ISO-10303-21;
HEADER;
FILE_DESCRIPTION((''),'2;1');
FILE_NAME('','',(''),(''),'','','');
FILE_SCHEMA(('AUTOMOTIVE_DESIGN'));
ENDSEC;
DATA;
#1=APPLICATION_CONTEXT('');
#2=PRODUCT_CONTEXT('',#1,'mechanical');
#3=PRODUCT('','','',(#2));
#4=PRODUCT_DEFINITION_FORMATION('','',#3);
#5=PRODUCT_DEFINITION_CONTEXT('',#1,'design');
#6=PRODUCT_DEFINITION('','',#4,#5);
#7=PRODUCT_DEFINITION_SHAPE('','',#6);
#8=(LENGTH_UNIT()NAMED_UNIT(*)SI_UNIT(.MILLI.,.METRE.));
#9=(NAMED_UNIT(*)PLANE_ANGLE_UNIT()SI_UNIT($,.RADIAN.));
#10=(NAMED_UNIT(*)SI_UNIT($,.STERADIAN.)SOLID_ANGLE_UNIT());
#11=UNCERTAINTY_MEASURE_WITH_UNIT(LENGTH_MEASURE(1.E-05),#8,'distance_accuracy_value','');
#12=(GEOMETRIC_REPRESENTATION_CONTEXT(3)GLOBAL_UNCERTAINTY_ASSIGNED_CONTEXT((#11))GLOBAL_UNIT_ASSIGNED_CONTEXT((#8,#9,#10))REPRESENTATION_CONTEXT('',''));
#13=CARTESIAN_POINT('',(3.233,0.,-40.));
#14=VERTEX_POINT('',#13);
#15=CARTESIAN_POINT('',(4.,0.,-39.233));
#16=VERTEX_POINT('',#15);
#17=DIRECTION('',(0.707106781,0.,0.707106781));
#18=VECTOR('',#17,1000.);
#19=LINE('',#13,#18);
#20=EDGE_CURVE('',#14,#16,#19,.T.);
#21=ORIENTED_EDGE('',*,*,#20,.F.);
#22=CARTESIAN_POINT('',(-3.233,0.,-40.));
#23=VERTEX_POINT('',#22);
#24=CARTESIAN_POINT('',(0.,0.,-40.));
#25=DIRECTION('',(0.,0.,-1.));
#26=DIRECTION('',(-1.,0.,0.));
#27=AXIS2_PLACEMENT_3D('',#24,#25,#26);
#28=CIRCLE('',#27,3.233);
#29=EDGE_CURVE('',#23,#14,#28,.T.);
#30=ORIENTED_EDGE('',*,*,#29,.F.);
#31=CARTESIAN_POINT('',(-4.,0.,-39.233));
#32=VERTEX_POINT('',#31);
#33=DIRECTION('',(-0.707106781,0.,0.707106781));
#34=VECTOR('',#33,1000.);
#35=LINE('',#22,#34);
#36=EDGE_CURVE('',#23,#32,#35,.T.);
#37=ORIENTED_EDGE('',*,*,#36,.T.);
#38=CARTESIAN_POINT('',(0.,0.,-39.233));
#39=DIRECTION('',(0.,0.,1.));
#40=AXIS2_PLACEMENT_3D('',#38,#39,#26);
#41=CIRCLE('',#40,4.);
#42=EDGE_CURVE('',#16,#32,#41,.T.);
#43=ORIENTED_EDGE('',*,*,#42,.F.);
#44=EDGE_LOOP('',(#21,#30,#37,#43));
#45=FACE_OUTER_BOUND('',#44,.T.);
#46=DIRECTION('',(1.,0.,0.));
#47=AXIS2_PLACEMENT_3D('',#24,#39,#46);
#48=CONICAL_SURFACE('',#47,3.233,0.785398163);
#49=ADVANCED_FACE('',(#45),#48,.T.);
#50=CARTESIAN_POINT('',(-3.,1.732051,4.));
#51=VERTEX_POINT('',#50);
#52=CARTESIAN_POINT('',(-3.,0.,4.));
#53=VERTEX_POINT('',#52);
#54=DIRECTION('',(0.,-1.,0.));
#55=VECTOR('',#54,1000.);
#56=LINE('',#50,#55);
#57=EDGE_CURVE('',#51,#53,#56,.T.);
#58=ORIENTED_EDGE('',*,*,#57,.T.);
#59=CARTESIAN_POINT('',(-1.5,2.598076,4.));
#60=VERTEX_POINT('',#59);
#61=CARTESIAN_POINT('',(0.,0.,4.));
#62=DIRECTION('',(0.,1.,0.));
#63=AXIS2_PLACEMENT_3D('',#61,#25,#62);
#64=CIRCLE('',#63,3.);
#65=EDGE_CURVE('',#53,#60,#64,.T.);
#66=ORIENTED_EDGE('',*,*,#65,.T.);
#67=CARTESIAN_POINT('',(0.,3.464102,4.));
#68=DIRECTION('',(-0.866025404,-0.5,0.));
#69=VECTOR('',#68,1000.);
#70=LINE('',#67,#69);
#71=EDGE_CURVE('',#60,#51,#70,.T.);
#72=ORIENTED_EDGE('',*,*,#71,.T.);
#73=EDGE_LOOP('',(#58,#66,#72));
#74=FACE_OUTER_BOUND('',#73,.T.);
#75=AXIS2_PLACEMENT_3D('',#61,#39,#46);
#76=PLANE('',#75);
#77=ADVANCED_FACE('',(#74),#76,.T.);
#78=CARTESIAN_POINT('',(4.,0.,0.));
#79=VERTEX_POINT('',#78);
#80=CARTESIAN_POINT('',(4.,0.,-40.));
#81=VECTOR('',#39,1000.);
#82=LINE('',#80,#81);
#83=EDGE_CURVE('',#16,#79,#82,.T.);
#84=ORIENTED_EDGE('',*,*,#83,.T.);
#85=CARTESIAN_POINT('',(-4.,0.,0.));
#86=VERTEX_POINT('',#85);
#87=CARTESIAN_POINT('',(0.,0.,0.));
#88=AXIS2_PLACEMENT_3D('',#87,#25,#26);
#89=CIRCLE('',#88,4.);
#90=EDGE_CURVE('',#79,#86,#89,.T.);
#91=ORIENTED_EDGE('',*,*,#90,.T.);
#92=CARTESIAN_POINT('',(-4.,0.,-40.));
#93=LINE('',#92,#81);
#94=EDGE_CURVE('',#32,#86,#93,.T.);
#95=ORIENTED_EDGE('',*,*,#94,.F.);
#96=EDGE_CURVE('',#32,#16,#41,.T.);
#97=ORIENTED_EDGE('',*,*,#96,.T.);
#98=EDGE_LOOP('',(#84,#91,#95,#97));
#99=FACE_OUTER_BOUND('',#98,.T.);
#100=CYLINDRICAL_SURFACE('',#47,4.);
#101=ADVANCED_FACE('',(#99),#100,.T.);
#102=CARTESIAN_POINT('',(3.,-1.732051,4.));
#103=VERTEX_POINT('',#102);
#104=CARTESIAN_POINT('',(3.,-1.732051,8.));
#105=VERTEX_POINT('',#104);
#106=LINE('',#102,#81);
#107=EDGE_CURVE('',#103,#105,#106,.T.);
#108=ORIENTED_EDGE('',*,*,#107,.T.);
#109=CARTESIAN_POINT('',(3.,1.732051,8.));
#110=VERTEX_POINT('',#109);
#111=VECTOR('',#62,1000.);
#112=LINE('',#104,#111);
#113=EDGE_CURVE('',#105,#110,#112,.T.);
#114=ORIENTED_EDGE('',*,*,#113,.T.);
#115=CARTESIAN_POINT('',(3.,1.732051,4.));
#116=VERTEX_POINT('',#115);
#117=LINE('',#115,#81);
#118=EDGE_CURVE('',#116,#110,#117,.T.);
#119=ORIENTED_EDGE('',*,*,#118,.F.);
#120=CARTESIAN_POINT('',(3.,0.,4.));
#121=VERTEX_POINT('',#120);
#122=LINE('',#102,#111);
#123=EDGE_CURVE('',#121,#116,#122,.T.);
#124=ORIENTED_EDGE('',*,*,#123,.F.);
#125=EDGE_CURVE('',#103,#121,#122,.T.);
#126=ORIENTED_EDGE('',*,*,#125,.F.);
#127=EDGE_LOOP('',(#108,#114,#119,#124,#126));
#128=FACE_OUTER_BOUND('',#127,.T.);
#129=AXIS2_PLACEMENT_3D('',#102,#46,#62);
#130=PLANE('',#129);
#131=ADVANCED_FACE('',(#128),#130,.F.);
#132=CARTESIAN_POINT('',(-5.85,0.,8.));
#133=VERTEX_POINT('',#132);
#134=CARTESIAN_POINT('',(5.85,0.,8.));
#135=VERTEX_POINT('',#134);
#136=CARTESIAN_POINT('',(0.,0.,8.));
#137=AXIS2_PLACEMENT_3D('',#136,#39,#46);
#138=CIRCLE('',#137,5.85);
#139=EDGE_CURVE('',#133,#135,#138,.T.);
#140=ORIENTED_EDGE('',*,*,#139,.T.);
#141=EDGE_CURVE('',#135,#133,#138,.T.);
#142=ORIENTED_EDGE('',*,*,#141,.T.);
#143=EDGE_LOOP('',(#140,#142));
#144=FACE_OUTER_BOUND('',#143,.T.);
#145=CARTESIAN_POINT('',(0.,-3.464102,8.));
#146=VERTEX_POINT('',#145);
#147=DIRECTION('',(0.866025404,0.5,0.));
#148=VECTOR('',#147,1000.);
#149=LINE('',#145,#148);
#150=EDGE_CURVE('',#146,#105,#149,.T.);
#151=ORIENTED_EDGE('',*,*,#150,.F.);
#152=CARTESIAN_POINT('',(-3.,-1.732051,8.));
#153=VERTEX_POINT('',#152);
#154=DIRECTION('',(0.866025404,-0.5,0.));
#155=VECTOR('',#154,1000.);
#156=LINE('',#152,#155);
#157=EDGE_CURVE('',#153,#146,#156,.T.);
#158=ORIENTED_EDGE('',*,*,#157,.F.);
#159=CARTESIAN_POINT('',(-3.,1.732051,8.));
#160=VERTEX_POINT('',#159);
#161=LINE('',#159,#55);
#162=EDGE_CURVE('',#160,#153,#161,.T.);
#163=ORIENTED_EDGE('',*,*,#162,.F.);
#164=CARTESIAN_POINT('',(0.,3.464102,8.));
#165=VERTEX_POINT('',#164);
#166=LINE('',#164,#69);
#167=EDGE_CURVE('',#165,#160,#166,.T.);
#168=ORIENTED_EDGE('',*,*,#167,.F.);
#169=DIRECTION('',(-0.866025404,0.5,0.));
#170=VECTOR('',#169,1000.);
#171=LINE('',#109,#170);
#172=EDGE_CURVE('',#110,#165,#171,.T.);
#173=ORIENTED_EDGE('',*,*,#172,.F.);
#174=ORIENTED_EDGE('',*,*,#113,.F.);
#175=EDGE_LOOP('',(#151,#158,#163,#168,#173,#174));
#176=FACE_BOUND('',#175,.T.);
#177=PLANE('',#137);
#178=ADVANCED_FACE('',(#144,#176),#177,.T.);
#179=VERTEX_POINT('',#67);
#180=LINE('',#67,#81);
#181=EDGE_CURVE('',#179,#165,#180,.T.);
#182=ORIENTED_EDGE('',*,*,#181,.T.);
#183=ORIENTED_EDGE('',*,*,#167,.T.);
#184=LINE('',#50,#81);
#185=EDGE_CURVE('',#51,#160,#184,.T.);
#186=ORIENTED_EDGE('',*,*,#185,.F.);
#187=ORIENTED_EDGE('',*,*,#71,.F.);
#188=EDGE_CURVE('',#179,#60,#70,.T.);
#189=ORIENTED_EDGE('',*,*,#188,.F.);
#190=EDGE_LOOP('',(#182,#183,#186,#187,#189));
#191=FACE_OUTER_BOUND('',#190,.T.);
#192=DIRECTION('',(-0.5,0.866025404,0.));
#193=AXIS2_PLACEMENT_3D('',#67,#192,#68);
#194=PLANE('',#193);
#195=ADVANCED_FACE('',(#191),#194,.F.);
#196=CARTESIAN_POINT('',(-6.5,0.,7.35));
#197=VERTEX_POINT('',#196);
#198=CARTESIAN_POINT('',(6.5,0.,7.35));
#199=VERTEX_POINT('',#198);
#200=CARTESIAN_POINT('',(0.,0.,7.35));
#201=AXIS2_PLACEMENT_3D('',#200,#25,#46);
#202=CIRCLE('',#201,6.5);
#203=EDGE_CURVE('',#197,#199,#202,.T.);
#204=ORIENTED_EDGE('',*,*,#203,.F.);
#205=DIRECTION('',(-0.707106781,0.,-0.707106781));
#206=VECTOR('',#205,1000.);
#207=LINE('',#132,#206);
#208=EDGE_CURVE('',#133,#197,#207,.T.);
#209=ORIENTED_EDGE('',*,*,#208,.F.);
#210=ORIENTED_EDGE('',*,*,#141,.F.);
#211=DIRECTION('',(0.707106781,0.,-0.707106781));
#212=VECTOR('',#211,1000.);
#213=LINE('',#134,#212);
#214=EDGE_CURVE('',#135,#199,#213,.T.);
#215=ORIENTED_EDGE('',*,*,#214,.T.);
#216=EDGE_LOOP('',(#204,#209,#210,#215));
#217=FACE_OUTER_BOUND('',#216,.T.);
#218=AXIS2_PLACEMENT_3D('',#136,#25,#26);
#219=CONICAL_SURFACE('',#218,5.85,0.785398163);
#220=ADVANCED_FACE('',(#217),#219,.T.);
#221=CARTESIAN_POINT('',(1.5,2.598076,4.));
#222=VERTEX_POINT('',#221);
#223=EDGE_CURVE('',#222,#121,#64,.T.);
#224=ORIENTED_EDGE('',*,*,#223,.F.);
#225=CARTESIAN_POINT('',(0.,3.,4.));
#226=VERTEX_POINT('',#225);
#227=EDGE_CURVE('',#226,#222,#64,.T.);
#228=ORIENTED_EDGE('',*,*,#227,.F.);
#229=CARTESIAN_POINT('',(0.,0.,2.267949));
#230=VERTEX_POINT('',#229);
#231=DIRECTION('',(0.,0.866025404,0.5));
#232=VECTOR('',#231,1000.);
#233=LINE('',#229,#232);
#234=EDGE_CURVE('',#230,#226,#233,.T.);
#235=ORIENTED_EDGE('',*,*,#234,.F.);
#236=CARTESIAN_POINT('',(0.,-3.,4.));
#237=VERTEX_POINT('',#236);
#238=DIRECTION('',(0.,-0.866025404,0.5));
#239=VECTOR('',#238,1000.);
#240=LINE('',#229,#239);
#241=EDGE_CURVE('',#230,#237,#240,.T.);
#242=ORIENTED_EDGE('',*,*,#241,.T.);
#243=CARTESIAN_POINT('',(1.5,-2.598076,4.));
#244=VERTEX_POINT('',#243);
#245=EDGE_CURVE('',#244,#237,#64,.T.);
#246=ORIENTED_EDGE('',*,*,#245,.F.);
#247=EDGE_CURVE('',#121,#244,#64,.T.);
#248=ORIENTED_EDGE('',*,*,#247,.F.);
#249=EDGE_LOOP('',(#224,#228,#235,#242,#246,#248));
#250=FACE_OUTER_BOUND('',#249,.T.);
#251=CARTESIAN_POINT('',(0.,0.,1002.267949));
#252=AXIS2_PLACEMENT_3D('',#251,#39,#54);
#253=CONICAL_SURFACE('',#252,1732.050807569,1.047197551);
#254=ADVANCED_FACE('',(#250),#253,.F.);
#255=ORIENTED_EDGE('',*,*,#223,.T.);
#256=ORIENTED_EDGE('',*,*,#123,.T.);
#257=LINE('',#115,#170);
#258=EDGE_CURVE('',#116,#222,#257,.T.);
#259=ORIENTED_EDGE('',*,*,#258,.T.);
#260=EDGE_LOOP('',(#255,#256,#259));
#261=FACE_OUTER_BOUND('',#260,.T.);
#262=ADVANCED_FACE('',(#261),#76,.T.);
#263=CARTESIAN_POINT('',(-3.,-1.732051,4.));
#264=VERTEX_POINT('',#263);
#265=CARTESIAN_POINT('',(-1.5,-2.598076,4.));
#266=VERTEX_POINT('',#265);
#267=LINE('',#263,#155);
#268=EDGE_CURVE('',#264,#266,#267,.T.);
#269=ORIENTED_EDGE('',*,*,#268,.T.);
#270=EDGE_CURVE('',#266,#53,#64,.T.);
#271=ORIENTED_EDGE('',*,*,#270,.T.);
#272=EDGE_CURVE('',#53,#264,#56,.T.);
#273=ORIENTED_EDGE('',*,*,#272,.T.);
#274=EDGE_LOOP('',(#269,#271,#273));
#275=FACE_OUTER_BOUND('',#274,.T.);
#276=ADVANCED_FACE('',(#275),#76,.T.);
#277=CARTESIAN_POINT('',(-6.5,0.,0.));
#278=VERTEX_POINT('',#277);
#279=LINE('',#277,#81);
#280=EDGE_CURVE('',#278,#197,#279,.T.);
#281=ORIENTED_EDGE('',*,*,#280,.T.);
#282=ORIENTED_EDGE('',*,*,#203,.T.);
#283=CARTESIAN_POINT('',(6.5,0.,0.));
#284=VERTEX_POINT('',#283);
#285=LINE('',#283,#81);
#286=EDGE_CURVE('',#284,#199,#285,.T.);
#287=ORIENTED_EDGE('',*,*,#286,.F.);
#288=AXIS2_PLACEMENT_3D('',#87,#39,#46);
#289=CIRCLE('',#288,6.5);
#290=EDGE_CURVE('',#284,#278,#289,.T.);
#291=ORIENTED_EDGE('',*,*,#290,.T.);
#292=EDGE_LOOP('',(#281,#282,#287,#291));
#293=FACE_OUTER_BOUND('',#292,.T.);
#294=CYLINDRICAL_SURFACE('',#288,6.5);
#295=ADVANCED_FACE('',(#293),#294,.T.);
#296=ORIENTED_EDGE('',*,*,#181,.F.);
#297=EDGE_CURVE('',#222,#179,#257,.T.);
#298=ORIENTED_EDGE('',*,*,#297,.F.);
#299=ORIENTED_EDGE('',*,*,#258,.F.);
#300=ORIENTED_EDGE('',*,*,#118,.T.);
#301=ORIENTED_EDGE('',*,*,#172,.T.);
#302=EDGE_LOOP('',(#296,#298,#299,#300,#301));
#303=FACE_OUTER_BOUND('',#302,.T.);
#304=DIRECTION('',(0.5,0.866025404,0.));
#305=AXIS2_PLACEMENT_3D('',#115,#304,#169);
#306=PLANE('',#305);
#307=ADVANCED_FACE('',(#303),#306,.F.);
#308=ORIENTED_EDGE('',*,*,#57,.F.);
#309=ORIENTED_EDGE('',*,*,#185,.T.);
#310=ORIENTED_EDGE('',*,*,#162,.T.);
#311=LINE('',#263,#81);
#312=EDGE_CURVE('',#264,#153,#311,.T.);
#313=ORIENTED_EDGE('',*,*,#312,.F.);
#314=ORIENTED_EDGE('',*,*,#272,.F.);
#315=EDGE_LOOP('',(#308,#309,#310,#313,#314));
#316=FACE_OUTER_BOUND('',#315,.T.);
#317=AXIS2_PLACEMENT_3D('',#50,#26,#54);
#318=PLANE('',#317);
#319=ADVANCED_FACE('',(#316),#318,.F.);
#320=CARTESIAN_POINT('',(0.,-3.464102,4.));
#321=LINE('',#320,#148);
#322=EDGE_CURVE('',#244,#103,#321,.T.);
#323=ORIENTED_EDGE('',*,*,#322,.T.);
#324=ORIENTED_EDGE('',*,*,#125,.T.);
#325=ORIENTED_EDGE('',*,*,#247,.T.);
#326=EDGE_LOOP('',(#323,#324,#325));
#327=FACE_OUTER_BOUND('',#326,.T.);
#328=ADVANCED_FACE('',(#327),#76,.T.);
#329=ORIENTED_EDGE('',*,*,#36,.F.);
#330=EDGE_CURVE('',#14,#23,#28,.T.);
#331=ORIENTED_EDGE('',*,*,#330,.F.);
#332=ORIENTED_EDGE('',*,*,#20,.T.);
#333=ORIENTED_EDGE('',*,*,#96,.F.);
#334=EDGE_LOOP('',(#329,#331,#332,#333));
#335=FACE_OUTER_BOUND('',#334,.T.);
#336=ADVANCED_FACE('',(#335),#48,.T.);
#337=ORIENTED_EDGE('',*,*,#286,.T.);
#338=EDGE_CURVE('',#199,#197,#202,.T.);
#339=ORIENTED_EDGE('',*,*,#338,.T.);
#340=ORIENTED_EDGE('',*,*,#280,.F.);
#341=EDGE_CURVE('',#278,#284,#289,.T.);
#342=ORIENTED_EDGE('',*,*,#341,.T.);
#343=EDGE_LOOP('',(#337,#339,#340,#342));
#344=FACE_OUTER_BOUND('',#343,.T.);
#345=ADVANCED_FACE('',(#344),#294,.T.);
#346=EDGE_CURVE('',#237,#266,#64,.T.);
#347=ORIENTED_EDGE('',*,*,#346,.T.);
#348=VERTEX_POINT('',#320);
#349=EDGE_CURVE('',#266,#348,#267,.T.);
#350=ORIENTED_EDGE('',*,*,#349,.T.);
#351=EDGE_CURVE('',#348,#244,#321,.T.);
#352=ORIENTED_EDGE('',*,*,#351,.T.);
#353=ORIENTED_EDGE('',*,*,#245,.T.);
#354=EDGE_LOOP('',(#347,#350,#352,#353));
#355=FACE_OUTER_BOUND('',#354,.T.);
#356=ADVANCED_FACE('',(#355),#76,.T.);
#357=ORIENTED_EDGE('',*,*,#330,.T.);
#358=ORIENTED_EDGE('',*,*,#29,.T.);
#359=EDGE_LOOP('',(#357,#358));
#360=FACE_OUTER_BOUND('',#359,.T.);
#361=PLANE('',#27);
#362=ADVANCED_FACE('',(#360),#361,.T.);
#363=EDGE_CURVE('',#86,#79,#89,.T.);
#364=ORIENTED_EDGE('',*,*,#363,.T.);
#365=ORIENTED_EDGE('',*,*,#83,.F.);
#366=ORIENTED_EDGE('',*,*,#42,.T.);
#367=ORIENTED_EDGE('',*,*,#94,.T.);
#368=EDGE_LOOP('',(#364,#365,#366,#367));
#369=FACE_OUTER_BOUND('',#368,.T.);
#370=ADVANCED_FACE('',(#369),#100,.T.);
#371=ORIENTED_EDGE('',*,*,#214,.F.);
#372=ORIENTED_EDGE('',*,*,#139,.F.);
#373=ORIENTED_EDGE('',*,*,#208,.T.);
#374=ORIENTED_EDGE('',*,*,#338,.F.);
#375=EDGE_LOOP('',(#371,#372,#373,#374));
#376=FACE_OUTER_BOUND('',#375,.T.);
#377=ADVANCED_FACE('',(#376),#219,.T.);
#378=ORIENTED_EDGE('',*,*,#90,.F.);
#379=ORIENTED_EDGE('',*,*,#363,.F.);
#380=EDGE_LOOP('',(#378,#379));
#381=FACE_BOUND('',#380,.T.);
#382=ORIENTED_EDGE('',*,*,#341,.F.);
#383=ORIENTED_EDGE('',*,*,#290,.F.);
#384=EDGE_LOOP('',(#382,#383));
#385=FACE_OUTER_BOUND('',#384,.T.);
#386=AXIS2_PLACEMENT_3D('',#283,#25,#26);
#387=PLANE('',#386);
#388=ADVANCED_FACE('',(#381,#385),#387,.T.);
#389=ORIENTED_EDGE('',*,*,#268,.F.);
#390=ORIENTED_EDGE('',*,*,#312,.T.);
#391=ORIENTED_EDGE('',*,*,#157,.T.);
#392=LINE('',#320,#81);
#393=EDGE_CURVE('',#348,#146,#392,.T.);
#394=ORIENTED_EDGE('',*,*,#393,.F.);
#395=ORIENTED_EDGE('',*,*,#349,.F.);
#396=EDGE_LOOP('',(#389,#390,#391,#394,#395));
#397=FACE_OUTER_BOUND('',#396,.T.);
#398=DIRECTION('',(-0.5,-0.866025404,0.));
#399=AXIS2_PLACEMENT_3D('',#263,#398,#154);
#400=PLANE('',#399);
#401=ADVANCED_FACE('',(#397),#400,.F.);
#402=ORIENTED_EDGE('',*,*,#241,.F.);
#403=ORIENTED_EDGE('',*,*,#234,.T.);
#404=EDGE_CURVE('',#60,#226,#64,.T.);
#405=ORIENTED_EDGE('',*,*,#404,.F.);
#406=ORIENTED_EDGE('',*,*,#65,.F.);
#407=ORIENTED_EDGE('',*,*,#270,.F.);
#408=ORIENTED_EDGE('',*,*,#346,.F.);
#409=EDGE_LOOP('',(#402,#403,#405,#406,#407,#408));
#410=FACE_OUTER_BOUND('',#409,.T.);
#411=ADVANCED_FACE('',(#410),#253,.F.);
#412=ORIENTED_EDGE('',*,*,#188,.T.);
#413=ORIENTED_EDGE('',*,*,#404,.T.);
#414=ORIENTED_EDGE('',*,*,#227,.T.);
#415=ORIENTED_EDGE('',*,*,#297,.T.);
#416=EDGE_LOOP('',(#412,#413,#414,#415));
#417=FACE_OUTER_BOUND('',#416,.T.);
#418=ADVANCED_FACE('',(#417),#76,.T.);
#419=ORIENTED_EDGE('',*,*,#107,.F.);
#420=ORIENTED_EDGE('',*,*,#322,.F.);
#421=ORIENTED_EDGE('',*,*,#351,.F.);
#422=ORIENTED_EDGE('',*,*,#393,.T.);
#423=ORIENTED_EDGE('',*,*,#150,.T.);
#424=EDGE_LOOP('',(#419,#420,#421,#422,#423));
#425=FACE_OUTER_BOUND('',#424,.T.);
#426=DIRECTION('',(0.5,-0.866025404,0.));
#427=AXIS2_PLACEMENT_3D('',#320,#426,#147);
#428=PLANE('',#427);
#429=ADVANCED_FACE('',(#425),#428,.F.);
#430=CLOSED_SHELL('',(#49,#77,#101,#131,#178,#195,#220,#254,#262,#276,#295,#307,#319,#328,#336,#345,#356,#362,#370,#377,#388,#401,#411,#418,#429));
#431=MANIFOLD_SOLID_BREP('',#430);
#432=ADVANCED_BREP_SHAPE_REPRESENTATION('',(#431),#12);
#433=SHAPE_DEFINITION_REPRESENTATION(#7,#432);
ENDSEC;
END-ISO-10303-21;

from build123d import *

# Parameters (mm, degrees)
SKETCH_1_W          = 6.5
SKETCH_1_H          = 8
SKETCH_2_R          = 4
EXTRUDE_1_DEPTH     = 40
CUT_EXTRUDE_1_DEPTH = 4
CHAMFER_1_SIZE      = 0.65
CHAMFER_2_SIZE      = 0.767


with BuildPart() as part:
    # 草图1 → 旋转1 (revolve)
    with BuildSketch(Plane(origin=(0, 0, 0), x_dir=(1, 0, 0), z_dir=(0, 1, 0))):
        with Locations((3.25, -4)):
            Rectangle(SKETCH_1_W, SKETCH_1_H)
    revolve(axis=Axis((0, 0, 0), (0, 0, 1)))

    # 草图2 → 凸台-拉伸1 (add)
    with BuildSketch(Plane(origin=(0, 0, 0), x_dir=(-1, 0, 0), z_dir=(0, 0, -1))):
        Circle(SKETCH_2_R)
    extrude(amount=EXTRUDE_1_DEPTH)

    # 草图3 → 切除-拉伸1 (cut)
    with BuildSketch(Plane.XY.offset(8)):
        Polygon((3, 1.732050808), (0, 3.464101615), (-3, 1.732050808), (-3, -1.732050808), (0, -3.464101615), (3, -1.732050808), align=None)
    extrude(amount=-CUT_EXTRUDE_1_DEPTH, mode=Mode.SUBTRACT)

    # 草图4 → 切除-旋转1 (revolve, cut)
    with BuildSketch(Plane.XZ, mode=Mode.PRIVATE) as cut_revolve_1_sk:
        Polygon((3, 4), (0, 4), (0, 2.267949192), align=None)
    revolve(cut_revolve_1_sk.sketch.rotate(Axis((0, 0, 4), (0, 0, -1)), 90), axis=Axis((0, 0, 4), (0, 0, -1)), mode=Mode.SUBTRACT)

    # 倒角1
    chamfer_1_edges = [part.edges().sort_by_distance(p)[0] for p in [
        (-6.5, 0, 8),
    ]]
    chamfer(chamfer_1_edges, length=CHAMFER_1_SIZE)

    # 倒角2
    chamfer_2_edges = [part.edges().sort_by_distance(p)[0] for p in [
        (4, 0, -40),
    ]]
    chamfer(chamfer_2_edges, length=CHAMFER_2_SIZE)


solid = part.part
